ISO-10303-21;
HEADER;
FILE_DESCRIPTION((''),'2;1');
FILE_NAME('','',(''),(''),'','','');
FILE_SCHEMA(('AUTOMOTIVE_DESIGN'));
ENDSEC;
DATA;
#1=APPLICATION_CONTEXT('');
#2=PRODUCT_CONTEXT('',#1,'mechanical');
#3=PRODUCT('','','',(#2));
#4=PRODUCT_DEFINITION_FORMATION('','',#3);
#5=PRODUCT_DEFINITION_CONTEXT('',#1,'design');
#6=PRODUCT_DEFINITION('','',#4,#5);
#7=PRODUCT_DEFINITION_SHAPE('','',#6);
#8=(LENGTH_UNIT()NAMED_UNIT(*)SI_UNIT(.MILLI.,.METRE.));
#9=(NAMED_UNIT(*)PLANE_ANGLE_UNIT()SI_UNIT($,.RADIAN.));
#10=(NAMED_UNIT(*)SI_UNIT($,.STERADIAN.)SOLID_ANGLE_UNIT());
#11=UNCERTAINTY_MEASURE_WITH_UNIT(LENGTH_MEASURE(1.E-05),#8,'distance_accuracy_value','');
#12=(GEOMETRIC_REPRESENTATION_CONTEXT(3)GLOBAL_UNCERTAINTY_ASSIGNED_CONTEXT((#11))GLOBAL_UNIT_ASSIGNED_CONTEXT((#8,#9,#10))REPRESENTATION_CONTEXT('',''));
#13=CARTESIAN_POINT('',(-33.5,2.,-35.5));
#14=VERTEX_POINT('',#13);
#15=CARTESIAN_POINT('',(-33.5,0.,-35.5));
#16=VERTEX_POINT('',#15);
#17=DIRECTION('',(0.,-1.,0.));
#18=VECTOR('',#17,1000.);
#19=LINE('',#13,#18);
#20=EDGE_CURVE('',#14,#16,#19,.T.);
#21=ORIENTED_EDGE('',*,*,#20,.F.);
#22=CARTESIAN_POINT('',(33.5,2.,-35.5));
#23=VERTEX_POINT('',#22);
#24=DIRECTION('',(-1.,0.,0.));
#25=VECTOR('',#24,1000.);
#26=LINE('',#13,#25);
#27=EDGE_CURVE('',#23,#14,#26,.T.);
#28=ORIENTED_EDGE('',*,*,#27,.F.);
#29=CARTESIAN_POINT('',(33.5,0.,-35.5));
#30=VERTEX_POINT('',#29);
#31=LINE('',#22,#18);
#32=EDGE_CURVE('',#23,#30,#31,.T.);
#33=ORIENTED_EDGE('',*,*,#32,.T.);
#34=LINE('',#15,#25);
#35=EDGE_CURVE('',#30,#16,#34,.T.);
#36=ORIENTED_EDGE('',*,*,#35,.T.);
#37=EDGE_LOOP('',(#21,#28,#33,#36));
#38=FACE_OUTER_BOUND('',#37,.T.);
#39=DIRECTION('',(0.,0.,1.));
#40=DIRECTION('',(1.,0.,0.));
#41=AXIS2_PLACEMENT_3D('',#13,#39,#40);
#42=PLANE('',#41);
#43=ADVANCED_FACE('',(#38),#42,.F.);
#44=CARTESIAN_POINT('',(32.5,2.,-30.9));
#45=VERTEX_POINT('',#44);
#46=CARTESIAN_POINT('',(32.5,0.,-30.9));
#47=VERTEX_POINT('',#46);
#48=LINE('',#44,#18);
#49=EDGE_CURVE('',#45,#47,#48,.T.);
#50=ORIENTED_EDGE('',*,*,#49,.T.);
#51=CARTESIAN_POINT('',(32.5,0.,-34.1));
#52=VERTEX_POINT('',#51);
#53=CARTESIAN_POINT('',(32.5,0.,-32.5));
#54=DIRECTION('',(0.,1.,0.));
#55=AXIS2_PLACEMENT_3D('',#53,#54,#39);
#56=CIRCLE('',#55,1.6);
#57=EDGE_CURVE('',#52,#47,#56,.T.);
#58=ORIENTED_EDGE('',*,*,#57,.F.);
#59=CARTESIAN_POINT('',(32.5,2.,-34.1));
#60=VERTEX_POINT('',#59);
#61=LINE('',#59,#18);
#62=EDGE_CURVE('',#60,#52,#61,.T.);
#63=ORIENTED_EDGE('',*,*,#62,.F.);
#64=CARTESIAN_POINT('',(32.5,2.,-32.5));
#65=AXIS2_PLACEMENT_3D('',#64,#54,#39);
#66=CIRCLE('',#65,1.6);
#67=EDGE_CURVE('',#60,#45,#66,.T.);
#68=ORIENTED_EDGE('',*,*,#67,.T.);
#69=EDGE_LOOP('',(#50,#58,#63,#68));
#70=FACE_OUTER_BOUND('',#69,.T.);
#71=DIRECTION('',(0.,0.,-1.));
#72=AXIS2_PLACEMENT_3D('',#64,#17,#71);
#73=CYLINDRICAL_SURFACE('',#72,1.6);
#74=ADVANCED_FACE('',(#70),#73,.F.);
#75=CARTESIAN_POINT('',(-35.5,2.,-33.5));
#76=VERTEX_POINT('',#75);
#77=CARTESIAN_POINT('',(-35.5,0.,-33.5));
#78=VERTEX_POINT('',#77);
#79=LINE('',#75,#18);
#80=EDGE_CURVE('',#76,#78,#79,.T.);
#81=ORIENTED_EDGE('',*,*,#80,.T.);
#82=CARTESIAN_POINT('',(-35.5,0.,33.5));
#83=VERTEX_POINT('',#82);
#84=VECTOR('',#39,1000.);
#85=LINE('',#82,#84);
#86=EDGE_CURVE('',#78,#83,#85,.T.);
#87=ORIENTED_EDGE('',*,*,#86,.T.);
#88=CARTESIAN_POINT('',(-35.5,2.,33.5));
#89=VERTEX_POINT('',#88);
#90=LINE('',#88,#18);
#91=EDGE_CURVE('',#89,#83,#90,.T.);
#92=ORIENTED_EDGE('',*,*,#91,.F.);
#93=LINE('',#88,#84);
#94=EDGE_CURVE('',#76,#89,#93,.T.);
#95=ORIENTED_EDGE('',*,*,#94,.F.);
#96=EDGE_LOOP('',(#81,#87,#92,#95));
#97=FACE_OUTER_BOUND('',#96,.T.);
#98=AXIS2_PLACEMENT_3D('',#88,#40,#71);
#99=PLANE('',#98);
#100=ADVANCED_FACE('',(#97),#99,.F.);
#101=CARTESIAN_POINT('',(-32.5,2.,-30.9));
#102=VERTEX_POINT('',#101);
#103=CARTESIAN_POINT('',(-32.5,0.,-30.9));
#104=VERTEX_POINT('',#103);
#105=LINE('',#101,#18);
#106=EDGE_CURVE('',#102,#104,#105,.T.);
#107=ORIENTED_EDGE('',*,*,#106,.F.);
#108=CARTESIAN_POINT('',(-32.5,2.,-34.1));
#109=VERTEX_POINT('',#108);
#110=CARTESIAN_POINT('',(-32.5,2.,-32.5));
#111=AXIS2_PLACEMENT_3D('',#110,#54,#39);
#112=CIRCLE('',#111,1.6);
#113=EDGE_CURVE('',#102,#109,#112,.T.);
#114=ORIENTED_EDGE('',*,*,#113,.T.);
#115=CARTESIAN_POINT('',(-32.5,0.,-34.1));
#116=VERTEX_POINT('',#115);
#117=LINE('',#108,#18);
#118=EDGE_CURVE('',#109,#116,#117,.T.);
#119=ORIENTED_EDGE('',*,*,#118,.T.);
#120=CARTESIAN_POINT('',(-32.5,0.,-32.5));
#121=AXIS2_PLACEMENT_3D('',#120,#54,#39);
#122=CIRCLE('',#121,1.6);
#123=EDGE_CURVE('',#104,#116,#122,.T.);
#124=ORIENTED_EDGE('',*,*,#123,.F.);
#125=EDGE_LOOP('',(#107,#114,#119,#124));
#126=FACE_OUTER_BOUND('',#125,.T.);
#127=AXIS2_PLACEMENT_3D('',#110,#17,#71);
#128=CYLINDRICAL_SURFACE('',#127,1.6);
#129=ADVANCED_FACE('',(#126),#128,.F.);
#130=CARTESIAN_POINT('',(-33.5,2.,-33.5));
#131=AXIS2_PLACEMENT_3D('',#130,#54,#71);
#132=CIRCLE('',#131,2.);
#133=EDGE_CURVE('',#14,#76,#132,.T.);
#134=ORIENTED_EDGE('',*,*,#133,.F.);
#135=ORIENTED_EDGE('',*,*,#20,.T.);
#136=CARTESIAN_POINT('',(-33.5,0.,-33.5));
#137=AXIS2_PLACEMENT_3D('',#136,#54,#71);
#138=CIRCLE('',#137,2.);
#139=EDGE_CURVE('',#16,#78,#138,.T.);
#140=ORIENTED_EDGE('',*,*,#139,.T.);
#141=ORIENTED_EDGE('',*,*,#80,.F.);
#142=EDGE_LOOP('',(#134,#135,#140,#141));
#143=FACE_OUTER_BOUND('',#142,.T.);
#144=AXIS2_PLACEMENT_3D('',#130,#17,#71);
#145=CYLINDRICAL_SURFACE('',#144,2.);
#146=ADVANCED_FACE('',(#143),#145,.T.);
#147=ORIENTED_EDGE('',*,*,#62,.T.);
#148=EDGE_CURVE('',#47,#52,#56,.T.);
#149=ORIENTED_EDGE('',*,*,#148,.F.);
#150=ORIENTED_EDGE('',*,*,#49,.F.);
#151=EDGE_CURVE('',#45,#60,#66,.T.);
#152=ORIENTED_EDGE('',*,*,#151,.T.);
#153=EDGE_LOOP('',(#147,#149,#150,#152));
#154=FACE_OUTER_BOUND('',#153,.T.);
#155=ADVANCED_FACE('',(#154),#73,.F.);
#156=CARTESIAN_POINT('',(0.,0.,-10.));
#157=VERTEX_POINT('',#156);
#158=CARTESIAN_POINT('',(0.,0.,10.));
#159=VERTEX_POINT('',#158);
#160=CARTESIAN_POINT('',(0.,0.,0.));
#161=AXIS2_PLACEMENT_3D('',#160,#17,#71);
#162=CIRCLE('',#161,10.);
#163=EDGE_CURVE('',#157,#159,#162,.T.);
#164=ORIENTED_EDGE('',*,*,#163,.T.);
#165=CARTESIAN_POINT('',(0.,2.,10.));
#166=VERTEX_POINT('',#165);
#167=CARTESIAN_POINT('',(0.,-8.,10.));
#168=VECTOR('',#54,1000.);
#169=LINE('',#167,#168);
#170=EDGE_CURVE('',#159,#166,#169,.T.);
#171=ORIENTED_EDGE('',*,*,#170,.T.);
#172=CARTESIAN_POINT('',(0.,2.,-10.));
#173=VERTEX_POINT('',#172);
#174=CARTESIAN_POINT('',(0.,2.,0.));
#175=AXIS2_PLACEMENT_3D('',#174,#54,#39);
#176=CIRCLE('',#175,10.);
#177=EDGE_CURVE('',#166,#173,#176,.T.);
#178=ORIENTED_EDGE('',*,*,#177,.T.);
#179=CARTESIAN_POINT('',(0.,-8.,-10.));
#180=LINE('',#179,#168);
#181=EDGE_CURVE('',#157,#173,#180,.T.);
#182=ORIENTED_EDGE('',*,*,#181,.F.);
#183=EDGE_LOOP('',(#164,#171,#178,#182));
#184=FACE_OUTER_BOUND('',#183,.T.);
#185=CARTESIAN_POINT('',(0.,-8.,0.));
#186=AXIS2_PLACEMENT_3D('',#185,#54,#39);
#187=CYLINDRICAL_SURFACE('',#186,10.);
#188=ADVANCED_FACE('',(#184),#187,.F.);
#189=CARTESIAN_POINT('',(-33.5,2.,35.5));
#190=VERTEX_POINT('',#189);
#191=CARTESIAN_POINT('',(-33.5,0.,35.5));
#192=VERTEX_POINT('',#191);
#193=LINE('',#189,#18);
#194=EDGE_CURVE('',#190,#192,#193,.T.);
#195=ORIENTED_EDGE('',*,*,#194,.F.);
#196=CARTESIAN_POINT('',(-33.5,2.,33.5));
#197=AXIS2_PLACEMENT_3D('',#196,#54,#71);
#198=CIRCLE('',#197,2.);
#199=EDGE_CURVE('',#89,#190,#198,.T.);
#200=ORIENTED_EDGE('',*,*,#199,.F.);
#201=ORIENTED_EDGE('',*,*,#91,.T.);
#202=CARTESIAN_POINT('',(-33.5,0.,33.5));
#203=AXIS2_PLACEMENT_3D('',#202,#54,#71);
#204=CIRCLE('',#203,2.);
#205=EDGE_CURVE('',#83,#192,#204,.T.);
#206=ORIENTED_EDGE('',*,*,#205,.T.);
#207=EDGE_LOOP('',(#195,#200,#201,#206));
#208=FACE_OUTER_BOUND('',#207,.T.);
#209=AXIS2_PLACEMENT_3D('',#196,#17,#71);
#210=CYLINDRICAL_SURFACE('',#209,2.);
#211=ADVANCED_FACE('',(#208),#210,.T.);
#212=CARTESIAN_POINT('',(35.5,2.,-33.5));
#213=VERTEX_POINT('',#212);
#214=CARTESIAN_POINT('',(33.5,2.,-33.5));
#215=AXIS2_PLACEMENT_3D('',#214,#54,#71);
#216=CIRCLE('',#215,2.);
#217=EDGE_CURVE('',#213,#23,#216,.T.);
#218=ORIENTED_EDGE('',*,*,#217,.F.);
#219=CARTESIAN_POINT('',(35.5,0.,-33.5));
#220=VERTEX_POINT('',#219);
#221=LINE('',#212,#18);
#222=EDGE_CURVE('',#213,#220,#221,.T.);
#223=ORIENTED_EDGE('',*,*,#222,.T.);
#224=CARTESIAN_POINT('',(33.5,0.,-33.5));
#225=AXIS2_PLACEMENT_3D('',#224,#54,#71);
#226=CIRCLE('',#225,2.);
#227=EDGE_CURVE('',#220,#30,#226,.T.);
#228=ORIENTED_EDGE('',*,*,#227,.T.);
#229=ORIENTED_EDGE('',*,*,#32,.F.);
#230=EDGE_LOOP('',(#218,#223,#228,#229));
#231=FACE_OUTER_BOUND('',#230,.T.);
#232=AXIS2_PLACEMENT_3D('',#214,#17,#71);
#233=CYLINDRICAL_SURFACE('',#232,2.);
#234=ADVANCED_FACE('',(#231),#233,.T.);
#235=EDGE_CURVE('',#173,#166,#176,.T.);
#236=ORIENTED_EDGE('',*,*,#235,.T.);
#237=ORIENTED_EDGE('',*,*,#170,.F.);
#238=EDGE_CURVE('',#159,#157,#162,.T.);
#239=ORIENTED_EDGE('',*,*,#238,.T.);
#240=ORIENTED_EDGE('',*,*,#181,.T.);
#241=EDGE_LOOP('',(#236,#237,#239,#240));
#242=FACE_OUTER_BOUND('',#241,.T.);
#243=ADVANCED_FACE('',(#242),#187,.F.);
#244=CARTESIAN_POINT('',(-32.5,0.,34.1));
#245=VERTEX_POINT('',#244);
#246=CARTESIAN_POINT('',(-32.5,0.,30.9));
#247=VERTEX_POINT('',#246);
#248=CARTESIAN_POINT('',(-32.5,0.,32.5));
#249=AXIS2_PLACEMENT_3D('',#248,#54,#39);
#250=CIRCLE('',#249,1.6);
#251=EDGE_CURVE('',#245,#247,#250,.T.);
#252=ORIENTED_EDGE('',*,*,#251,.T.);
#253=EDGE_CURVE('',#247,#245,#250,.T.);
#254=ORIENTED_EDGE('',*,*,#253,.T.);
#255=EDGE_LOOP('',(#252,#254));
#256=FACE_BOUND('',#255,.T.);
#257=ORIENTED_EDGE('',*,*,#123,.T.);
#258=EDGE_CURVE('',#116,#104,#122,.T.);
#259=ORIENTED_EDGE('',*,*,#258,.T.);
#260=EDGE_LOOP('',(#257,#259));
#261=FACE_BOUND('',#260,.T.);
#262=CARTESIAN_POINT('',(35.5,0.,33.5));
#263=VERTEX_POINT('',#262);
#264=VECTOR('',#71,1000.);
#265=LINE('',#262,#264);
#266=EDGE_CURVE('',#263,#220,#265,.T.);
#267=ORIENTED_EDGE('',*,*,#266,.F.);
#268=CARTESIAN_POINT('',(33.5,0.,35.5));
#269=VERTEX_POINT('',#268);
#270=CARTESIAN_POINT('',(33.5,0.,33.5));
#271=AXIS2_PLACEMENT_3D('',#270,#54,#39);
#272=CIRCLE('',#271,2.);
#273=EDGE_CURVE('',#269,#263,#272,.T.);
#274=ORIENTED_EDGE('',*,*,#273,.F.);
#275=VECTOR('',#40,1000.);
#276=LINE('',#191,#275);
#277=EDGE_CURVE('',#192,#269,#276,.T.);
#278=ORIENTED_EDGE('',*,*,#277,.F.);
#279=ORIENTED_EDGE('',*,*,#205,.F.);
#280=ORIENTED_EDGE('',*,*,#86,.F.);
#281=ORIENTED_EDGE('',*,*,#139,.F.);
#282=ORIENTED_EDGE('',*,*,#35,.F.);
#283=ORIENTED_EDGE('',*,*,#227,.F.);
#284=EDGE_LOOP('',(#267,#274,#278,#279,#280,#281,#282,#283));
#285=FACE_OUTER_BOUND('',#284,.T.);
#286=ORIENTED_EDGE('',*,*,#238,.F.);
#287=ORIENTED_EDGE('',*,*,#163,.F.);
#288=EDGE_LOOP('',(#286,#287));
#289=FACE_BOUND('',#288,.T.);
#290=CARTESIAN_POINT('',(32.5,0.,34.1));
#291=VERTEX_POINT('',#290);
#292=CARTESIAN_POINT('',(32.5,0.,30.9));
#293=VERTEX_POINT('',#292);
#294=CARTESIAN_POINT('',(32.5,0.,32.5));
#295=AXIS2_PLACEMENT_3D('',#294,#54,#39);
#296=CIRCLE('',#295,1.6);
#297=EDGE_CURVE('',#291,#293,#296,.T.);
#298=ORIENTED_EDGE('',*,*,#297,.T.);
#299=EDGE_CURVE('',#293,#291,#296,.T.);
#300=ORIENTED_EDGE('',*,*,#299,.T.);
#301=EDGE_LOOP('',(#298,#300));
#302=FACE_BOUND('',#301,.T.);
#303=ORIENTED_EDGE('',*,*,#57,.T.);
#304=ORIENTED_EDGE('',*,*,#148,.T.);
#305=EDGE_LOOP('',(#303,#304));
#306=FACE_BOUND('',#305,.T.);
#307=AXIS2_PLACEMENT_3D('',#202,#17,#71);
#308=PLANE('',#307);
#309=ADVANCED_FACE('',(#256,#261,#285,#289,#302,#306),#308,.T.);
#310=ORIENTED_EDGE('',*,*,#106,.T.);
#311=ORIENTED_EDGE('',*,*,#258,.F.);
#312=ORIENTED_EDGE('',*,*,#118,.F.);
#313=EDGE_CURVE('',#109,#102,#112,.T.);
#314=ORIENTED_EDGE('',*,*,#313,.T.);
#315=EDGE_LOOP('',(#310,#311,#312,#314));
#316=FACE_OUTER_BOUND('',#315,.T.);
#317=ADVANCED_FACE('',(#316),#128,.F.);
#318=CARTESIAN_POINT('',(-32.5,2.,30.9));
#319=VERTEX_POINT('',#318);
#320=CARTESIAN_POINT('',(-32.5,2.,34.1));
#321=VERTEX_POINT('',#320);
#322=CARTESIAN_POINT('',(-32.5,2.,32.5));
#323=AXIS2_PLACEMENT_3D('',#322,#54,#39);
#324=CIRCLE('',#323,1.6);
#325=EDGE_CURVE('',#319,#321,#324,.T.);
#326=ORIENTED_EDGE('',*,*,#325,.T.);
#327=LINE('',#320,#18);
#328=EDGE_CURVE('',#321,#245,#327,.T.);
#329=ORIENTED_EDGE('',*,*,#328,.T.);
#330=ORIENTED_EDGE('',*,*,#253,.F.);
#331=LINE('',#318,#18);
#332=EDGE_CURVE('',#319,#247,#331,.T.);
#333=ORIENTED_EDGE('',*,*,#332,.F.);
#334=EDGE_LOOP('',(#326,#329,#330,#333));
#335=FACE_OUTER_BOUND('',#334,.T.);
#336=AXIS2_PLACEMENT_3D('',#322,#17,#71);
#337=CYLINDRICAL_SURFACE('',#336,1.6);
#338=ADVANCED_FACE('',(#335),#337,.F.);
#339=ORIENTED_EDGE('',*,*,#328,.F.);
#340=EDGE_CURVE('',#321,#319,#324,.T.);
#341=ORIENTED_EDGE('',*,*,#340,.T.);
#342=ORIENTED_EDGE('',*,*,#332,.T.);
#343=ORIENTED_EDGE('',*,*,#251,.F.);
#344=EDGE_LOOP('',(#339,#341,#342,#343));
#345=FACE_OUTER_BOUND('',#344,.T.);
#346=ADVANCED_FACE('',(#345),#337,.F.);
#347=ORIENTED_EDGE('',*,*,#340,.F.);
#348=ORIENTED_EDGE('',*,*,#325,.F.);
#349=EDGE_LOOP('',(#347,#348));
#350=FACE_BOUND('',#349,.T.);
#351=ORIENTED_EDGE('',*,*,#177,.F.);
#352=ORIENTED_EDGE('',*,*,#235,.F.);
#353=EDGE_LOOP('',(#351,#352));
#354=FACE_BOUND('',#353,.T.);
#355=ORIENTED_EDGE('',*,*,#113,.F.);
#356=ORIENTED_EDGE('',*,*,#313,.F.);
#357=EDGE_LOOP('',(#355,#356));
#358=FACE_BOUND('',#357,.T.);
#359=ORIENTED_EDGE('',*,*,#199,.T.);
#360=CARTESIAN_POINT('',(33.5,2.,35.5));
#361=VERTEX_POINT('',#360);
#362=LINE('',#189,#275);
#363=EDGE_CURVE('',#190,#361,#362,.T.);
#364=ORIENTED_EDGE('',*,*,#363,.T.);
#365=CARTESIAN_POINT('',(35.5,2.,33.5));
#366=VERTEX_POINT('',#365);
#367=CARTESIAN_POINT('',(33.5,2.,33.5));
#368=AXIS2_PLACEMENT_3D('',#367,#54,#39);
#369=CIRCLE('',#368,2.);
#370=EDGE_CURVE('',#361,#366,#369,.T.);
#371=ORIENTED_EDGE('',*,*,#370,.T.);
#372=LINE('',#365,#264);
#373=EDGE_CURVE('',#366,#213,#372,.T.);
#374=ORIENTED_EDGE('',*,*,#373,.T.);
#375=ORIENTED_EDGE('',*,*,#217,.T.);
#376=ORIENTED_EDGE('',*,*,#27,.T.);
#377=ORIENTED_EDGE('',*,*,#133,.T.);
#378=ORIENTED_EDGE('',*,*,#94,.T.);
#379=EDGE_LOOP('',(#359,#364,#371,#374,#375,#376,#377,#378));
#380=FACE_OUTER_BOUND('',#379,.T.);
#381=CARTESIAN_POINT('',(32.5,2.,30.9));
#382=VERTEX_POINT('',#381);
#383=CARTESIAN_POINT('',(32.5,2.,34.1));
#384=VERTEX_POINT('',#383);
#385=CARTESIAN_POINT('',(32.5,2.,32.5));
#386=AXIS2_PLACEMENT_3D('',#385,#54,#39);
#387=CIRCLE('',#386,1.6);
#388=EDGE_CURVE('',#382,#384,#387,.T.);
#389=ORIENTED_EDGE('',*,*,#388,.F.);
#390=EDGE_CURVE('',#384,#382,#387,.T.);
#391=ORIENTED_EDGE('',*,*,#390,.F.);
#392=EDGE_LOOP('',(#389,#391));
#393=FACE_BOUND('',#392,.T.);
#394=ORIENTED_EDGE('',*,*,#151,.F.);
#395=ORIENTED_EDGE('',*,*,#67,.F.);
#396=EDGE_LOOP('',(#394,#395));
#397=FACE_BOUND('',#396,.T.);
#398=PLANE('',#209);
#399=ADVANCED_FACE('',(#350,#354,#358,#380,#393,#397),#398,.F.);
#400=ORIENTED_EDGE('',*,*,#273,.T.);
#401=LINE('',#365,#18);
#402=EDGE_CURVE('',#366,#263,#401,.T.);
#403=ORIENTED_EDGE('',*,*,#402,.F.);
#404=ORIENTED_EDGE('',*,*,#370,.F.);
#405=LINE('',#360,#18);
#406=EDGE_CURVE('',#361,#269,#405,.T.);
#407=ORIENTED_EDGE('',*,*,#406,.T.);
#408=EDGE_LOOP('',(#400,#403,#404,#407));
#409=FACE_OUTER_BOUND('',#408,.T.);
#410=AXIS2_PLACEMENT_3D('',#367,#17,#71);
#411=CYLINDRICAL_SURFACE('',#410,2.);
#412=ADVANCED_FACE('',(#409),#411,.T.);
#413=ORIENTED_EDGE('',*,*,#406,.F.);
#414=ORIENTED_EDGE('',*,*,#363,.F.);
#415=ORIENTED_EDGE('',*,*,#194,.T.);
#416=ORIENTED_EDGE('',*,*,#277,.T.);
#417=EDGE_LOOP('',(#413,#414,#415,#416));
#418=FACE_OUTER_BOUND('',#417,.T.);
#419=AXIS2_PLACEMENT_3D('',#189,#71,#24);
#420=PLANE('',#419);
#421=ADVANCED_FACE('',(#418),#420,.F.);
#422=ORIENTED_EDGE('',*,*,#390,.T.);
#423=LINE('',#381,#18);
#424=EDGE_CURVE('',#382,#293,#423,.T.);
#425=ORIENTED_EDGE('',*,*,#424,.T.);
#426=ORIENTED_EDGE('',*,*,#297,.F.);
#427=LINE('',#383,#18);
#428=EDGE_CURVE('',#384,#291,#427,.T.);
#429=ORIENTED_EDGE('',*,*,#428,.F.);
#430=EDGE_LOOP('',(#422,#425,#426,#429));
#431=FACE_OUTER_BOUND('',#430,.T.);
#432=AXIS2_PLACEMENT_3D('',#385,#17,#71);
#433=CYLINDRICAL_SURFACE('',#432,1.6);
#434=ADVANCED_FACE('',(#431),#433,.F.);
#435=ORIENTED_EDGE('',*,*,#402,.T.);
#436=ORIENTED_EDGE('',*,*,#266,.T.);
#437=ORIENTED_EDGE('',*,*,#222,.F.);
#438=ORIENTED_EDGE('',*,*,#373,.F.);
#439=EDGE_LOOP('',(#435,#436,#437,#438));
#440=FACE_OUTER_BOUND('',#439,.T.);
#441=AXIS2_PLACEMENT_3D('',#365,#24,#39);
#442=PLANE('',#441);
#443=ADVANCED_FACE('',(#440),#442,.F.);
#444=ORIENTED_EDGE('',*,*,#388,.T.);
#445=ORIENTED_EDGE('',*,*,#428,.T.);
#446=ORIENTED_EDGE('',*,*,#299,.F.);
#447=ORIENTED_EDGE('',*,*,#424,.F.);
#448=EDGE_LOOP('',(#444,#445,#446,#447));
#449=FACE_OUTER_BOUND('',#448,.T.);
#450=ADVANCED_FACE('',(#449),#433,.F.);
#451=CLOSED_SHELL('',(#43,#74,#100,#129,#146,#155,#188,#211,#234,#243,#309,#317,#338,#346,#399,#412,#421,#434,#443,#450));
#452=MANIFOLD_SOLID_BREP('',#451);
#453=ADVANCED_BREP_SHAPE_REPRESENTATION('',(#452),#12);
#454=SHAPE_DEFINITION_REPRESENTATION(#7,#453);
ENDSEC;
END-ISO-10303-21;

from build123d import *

# Parameters (mm, degrees)
SKETCH1_R           = 1.6
BOSS_EXTRUDE1_DEPTH = 2
SKETCH2_R           = 10
CUT_EXTRUDE1_DEPTH  = 10


with BuildPart() as part:
    # Sketch1 → Boss-Extrude1 (new body)
    with BuildSketch(Plane(origin=(0, 0, 0), x_dir=(1, 0, 0), z_dir=(0, 1, 0))):
        with BuildLine():
            Line((-33.5, -35.5), (33.5, -35.5))
            ThreePointArc((33.5, -35.5), (34.914213562, -34.914213562), (35.5, -33.5))
            Line((35.5, -33.5), (35.5, 33.5))
            ThreePointArc((35.5, 33.5), (34.914213562, 34.914213562), (33.5, 35.5))
            Line((33.5, 35.5), (-33.5, 35.5))
            ThreePointArc((-33.5, 35.5), (-34.914213562, 34.914213562), (-35.5, 33.5))
            Line((-35.5, 33.5), (-35.5, -33.5))
            ThreePointArc((-35.5, -33.5), (-34.914213562, -34.914213562), (-33.5, -35.5))
        make_face()
        with Locations(Location((-32.5, 32.5, 0), (0, 0, 270))):
            Circle(SKETCH1_R, mode=Mode.SUBTRACT)
        with Locations(Location((32.5, 32.5, 0), (0, 0, 270))):
            Circle(SKETCH1_R, mode=Mode.SUBTRACT)
        with Locations(Location((32.5, -32.5, 0), (0, 0, 270))):
            Circle(SKETCH1_R, mode=Mode.SUBTRACT)
        with Locations(Location((-32.5, -32.5, 0), (0, 0, 270))):
            Circle(SKETCH1_R, mode=Mode.SUBTRACT)
    extrude(amount=BOSS_EXTRUDE1_DEPTH)

    # Sketch2 → Cut-Extrude1 (cut)
    with BuildSketch(Plane(origin=(0, 2, 0), x_dir=(1, 0, 0), z_dir=(0, 1, 0))):
        with Locations(Location((0, 0, 0), (0, 0, 270))):
            Circle(SKETCH2_R)
    extrude(amount=-CUT_EXTRUDE1_DEPTH, mode=Mode.SUBTRACT)


solid = part.part
